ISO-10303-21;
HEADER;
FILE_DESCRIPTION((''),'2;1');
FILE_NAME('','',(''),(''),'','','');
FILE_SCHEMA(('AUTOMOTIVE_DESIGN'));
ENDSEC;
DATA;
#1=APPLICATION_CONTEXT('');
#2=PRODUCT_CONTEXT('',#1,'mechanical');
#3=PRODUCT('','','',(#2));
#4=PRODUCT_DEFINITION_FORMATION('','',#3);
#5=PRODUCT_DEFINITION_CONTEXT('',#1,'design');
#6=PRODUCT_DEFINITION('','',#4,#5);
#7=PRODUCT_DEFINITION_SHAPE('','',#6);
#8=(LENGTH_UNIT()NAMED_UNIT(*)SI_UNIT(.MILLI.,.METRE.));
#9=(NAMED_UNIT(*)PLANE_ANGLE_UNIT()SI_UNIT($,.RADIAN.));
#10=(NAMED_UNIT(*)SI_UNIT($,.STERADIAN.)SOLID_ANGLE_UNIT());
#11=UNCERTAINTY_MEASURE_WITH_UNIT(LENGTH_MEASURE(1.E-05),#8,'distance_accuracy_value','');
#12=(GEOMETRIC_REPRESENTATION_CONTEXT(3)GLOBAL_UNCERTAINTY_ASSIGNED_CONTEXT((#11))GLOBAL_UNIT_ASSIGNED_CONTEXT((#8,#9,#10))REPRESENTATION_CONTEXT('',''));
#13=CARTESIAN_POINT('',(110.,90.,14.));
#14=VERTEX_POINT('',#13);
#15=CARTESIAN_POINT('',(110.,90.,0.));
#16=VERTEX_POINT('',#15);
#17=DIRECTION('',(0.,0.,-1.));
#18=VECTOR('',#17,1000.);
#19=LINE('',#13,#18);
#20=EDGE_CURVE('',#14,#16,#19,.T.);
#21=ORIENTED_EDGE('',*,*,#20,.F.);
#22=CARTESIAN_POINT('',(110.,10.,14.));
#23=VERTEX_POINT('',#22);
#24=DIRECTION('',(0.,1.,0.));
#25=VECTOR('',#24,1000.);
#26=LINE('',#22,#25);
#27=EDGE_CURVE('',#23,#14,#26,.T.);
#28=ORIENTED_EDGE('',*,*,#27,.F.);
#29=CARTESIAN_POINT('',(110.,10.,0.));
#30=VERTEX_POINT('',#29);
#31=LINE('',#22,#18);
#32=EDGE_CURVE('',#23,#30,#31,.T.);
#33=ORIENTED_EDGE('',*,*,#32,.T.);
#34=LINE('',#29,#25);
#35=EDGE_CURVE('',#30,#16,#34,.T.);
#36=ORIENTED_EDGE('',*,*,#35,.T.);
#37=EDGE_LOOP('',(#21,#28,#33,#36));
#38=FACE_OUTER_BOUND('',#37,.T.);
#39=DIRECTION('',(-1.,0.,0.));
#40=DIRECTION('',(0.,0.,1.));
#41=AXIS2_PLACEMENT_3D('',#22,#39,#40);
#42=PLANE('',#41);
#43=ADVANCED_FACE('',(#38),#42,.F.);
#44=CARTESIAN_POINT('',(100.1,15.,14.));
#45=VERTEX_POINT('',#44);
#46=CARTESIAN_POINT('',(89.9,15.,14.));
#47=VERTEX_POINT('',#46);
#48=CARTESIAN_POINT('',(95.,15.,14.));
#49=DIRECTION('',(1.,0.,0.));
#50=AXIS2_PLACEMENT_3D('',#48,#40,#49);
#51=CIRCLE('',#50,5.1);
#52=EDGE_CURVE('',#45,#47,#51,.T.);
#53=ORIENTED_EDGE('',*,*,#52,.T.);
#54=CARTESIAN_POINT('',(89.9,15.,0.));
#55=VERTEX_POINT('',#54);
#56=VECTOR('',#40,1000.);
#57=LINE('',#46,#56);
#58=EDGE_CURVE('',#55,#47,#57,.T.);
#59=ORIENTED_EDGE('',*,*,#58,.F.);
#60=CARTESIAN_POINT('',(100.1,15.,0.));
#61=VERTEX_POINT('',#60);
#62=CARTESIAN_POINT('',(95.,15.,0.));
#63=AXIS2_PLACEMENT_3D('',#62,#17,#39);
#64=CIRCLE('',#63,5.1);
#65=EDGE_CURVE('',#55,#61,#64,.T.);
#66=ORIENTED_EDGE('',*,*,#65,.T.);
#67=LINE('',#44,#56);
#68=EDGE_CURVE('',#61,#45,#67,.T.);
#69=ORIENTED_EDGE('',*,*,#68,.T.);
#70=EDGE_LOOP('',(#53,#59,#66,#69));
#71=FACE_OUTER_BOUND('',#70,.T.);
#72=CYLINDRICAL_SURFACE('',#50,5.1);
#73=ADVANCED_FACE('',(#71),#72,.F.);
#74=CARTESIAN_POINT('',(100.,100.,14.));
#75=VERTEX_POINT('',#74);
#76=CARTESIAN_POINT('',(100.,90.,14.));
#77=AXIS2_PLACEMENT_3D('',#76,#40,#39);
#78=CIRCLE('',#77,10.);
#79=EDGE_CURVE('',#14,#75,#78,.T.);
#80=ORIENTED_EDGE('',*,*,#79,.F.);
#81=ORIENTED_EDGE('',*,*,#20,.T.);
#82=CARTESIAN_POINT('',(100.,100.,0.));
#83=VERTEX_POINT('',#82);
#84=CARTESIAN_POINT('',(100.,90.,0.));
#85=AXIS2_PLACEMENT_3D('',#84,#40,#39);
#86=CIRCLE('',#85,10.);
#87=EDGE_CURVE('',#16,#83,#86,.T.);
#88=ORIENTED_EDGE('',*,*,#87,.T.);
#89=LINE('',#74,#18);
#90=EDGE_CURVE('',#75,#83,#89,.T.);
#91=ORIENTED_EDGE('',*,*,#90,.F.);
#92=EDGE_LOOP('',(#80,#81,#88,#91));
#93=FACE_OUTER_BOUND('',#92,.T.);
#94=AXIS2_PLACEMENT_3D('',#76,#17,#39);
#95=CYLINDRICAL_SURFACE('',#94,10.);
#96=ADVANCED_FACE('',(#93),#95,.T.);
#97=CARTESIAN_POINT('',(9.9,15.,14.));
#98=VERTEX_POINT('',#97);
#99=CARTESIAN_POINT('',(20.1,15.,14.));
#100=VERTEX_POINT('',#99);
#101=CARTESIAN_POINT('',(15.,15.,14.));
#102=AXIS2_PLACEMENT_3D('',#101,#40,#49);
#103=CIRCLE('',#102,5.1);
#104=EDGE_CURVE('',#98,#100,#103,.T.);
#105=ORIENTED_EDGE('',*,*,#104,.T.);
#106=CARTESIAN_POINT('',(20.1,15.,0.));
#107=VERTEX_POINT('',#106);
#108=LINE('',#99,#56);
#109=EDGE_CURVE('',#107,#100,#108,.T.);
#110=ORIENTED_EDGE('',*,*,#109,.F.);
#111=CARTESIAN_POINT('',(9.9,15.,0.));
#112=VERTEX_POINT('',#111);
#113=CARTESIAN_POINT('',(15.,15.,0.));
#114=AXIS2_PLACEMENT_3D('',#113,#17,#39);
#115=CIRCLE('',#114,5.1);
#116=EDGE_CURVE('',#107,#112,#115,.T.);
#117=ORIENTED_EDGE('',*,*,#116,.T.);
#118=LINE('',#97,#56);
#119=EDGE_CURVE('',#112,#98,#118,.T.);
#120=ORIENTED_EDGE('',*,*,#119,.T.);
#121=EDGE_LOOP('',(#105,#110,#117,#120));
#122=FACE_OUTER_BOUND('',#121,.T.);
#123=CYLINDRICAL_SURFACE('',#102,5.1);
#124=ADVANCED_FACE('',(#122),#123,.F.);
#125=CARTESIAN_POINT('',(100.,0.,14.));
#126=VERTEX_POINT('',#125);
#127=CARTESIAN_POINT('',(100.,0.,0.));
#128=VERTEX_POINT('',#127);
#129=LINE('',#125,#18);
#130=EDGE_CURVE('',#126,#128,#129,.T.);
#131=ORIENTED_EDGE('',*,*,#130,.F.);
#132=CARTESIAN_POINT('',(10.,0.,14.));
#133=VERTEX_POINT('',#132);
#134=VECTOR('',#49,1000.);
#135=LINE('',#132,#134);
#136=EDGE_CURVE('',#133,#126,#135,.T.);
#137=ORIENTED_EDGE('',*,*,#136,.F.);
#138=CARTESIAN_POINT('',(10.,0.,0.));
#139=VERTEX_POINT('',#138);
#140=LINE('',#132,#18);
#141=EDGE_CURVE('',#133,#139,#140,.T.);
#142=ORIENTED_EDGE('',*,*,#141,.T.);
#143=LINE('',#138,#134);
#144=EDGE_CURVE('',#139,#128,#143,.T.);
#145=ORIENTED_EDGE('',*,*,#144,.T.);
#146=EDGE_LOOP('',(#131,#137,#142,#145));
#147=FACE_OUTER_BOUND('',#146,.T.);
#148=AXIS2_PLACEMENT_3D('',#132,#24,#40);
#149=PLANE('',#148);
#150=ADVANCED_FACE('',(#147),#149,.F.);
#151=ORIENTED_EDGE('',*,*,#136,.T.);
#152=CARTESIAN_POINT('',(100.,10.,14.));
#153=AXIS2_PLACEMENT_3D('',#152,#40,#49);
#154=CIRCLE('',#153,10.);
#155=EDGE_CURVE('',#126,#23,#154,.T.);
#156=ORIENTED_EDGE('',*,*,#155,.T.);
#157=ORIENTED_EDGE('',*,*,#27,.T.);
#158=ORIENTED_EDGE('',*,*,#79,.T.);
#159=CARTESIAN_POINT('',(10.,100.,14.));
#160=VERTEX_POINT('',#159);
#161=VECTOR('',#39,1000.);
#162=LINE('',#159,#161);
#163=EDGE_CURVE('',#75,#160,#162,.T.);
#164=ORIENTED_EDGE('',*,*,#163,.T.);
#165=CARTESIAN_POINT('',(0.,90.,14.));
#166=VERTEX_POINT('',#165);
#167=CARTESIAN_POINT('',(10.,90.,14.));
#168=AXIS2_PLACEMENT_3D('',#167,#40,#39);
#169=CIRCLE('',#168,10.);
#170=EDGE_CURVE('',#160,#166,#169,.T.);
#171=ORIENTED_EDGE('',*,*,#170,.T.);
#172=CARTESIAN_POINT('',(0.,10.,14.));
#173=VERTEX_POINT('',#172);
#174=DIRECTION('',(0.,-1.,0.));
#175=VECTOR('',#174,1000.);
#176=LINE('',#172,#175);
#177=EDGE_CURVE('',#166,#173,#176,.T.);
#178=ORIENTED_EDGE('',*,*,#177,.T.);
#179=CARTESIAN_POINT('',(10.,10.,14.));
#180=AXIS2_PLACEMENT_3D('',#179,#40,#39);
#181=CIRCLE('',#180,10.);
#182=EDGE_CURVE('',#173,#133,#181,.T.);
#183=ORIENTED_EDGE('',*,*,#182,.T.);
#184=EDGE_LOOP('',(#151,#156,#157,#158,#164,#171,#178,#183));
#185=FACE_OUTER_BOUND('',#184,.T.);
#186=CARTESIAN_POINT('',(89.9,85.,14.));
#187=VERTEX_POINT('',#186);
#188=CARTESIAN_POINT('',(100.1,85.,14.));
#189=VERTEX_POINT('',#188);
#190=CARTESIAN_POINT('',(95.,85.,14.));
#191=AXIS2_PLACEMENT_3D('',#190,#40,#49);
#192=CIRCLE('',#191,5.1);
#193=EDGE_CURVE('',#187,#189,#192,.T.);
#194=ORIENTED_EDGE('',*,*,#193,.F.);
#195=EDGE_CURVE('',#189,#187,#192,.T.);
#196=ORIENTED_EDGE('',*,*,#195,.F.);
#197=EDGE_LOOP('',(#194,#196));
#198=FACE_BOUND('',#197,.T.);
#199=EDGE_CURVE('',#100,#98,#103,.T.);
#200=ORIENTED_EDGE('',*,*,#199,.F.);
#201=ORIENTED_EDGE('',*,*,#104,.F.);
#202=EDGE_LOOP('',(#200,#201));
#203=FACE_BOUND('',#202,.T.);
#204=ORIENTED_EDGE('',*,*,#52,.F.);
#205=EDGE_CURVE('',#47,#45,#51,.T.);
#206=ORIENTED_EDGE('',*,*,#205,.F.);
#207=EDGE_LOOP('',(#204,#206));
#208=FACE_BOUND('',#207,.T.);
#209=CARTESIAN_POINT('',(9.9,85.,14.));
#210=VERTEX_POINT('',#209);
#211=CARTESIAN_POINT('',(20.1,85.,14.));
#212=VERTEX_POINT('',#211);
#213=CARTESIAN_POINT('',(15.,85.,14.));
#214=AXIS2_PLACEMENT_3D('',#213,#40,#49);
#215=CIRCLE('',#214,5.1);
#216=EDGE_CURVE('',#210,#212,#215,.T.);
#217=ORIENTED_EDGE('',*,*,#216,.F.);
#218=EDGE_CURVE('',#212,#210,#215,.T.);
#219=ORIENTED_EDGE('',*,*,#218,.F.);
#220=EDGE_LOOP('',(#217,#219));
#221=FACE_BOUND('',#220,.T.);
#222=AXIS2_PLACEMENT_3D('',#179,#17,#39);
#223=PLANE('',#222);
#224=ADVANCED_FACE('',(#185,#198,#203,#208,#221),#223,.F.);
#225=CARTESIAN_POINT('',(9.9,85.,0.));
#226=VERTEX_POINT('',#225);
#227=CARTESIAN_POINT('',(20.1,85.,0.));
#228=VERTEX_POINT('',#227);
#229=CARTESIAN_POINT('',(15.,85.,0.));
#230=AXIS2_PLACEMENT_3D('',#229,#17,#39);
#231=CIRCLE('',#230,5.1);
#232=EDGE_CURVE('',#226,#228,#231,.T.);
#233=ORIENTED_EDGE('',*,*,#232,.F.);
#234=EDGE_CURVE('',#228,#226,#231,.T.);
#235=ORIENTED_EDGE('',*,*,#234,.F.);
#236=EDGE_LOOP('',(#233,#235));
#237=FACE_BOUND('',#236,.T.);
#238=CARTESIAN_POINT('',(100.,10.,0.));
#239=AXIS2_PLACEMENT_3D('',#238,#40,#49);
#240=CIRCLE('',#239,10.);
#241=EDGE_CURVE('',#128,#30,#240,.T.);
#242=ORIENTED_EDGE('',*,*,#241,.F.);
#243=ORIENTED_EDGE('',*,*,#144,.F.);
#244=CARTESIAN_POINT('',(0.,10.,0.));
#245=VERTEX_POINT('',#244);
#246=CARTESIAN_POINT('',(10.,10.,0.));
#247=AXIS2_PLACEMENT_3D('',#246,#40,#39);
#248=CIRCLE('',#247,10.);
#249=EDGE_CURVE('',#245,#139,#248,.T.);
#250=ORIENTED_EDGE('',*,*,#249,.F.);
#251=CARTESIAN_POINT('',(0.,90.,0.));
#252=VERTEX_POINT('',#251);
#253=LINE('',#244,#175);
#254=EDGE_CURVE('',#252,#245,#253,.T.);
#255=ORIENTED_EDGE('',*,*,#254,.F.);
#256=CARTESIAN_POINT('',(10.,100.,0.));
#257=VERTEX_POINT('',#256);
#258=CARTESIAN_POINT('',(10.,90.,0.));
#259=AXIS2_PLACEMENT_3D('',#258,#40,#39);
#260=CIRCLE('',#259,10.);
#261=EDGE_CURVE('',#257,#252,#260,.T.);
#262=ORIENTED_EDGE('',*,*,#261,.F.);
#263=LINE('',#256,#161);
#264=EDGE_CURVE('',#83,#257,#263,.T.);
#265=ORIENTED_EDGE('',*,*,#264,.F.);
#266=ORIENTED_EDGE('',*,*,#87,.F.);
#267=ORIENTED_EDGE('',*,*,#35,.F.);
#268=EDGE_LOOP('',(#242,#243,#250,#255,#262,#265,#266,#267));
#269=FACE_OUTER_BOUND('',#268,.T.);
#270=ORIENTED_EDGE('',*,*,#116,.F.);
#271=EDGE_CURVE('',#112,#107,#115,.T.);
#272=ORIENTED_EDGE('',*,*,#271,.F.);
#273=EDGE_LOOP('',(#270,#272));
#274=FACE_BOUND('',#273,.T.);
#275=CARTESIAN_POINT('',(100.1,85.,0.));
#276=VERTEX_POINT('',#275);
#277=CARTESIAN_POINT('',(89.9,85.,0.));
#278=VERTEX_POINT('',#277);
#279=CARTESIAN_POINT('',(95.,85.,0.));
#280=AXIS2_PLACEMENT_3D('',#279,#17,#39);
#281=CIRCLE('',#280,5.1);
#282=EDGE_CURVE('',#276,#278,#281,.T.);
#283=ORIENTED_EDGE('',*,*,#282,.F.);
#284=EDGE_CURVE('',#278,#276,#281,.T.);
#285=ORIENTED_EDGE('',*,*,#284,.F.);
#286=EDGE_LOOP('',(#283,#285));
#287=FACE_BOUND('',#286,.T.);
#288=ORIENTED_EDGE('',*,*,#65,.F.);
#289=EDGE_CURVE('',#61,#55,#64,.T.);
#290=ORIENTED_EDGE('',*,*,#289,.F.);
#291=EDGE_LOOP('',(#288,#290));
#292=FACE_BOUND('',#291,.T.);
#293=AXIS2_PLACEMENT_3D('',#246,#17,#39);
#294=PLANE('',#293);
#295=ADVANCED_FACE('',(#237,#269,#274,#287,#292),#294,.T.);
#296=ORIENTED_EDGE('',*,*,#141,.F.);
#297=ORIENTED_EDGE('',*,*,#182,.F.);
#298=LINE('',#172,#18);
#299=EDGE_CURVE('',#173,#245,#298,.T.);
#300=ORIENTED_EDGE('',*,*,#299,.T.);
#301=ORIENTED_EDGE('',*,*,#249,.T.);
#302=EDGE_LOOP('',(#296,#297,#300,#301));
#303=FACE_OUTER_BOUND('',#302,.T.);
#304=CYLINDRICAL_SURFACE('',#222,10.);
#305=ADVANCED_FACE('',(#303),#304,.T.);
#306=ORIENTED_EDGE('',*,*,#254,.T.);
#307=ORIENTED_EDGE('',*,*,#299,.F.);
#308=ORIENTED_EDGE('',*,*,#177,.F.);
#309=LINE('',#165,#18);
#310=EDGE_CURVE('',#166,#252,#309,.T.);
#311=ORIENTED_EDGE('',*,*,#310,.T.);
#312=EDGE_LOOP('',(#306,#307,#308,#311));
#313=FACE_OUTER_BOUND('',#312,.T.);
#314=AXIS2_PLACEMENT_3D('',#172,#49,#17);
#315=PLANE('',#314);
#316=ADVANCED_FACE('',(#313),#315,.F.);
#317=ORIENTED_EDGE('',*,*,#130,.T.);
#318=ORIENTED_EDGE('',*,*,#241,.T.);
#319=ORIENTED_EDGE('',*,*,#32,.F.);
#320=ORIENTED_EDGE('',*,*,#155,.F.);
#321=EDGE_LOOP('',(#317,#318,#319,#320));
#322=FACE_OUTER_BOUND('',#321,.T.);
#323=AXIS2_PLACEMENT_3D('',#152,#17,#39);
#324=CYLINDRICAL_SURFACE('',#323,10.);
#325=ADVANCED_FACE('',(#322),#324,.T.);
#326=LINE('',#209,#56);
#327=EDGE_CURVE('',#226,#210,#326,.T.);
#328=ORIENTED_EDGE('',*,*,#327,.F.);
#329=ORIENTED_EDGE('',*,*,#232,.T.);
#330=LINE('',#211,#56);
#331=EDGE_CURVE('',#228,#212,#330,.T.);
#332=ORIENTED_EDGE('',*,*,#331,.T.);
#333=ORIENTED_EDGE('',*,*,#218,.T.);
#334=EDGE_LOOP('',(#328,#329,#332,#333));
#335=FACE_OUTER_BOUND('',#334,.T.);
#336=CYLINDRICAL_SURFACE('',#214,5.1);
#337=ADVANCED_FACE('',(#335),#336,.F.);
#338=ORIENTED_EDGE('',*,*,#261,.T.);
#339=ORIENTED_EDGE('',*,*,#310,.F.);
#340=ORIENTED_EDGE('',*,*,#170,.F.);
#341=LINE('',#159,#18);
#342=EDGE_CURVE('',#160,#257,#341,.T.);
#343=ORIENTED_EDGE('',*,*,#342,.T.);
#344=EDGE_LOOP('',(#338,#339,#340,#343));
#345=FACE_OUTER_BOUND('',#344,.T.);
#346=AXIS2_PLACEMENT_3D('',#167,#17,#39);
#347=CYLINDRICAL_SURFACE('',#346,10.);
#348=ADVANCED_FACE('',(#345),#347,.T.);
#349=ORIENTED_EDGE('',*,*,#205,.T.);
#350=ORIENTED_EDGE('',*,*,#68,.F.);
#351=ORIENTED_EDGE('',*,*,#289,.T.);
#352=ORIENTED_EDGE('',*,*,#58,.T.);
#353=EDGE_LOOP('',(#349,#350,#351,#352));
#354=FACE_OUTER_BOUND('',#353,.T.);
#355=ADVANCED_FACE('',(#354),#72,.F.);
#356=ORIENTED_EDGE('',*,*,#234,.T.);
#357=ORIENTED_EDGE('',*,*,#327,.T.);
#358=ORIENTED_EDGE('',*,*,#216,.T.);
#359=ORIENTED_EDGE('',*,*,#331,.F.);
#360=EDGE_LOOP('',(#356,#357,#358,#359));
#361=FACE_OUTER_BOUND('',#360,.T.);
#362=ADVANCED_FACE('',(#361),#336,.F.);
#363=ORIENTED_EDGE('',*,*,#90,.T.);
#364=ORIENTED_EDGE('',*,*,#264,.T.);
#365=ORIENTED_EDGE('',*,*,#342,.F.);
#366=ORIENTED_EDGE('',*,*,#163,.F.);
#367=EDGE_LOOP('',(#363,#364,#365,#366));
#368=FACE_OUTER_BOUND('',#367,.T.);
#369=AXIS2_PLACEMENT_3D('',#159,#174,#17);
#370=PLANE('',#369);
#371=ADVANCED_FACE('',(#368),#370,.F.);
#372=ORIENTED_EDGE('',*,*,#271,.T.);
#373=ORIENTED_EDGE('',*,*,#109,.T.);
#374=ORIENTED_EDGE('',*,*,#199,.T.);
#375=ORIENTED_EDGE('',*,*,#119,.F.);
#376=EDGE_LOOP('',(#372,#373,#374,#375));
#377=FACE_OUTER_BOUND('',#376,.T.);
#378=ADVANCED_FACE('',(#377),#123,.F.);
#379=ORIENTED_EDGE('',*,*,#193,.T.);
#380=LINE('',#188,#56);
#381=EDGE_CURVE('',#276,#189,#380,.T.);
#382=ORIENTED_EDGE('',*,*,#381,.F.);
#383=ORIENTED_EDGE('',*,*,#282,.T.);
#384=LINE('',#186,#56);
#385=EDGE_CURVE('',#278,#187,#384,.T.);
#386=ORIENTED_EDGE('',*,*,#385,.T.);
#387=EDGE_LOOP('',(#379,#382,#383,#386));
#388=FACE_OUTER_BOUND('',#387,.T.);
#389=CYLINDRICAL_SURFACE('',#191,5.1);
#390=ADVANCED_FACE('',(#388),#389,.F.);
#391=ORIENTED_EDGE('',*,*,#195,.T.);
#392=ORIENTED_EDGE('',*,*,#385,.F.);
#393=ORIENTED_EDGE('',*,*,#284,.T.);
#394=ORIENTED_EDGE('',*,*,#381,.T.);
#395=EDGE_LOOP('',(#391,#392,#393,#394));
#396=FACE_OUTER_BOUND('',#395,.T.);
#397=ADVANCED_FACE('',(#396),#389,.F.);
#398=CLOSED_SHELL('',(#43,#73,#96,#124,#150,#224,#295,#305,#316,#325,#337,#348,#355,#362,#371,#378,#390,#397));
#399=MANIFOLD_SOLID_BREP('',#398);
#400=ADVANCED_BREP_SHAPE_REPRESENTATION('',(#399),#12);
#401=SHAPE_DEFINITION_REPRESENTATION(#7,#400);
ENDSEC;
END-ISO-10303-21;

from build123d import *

# Parameters (mm, degrees)
EXTRUDE_1_DEPTH         = 14
HOLE_WIZARD_M12_1_D     = 10.2
HOLE_WIZARD_M12_1_DEPTH = 29.25
HOLE_WIZARD_M12_1_TIP   = 3.064389157


with BuildPart() as part:
    # 草图1 → 凸台-拉伸1 (new body)
    with BuildSketch(Plane.XY):
        with BuildLine():
            Line((10, 0), (100, 0))
            ThreePointArc((100, 0), (107.071067812, 2.928932188), (110, 10))
            Line((110, 10), (110, 90))
            ThreePointArc((110, 90), (107.071067812, 97.071067812), (100, 100))
            Line((100, 100), (10, 100))
            ThreePointArc((10, 100), (2.928932188, 97.071067812), (0, 90))
            Line((0, 90), (0, 10))
            ThreePointArc((0, 10), (2.928932188, 2.928932188), (10, 0))
        make_face()
    extrude(amount=EXTRUDE_1_DEPTH)

    # M12 螺纹孔1
    with Locations(Plane(origin=(15, 85, 14), x_dir=(1, 0, 0), z_dir=(0, 0, 1))):
        with Locations((0, 0), (80, 0), (80, -70), (0, -70)):
            Hole(HOLE_WIZARD_M12_1_D / 2, depth=HOLE_WIZARD_M12_1_DEPTH)
            with Locations((0, 0, -(HOLE_WIZARD_M12_1_DEPTH + HOLE_WIZARD_M12_1_TIP / 2))):  # 118° drill point
                Cone(0, HOLE_WIZARD_M12_1_D / 2, HOLE_WIZARD_M12_1_TIP, mode=Mode.SUBTRACT)


solid = part.part
